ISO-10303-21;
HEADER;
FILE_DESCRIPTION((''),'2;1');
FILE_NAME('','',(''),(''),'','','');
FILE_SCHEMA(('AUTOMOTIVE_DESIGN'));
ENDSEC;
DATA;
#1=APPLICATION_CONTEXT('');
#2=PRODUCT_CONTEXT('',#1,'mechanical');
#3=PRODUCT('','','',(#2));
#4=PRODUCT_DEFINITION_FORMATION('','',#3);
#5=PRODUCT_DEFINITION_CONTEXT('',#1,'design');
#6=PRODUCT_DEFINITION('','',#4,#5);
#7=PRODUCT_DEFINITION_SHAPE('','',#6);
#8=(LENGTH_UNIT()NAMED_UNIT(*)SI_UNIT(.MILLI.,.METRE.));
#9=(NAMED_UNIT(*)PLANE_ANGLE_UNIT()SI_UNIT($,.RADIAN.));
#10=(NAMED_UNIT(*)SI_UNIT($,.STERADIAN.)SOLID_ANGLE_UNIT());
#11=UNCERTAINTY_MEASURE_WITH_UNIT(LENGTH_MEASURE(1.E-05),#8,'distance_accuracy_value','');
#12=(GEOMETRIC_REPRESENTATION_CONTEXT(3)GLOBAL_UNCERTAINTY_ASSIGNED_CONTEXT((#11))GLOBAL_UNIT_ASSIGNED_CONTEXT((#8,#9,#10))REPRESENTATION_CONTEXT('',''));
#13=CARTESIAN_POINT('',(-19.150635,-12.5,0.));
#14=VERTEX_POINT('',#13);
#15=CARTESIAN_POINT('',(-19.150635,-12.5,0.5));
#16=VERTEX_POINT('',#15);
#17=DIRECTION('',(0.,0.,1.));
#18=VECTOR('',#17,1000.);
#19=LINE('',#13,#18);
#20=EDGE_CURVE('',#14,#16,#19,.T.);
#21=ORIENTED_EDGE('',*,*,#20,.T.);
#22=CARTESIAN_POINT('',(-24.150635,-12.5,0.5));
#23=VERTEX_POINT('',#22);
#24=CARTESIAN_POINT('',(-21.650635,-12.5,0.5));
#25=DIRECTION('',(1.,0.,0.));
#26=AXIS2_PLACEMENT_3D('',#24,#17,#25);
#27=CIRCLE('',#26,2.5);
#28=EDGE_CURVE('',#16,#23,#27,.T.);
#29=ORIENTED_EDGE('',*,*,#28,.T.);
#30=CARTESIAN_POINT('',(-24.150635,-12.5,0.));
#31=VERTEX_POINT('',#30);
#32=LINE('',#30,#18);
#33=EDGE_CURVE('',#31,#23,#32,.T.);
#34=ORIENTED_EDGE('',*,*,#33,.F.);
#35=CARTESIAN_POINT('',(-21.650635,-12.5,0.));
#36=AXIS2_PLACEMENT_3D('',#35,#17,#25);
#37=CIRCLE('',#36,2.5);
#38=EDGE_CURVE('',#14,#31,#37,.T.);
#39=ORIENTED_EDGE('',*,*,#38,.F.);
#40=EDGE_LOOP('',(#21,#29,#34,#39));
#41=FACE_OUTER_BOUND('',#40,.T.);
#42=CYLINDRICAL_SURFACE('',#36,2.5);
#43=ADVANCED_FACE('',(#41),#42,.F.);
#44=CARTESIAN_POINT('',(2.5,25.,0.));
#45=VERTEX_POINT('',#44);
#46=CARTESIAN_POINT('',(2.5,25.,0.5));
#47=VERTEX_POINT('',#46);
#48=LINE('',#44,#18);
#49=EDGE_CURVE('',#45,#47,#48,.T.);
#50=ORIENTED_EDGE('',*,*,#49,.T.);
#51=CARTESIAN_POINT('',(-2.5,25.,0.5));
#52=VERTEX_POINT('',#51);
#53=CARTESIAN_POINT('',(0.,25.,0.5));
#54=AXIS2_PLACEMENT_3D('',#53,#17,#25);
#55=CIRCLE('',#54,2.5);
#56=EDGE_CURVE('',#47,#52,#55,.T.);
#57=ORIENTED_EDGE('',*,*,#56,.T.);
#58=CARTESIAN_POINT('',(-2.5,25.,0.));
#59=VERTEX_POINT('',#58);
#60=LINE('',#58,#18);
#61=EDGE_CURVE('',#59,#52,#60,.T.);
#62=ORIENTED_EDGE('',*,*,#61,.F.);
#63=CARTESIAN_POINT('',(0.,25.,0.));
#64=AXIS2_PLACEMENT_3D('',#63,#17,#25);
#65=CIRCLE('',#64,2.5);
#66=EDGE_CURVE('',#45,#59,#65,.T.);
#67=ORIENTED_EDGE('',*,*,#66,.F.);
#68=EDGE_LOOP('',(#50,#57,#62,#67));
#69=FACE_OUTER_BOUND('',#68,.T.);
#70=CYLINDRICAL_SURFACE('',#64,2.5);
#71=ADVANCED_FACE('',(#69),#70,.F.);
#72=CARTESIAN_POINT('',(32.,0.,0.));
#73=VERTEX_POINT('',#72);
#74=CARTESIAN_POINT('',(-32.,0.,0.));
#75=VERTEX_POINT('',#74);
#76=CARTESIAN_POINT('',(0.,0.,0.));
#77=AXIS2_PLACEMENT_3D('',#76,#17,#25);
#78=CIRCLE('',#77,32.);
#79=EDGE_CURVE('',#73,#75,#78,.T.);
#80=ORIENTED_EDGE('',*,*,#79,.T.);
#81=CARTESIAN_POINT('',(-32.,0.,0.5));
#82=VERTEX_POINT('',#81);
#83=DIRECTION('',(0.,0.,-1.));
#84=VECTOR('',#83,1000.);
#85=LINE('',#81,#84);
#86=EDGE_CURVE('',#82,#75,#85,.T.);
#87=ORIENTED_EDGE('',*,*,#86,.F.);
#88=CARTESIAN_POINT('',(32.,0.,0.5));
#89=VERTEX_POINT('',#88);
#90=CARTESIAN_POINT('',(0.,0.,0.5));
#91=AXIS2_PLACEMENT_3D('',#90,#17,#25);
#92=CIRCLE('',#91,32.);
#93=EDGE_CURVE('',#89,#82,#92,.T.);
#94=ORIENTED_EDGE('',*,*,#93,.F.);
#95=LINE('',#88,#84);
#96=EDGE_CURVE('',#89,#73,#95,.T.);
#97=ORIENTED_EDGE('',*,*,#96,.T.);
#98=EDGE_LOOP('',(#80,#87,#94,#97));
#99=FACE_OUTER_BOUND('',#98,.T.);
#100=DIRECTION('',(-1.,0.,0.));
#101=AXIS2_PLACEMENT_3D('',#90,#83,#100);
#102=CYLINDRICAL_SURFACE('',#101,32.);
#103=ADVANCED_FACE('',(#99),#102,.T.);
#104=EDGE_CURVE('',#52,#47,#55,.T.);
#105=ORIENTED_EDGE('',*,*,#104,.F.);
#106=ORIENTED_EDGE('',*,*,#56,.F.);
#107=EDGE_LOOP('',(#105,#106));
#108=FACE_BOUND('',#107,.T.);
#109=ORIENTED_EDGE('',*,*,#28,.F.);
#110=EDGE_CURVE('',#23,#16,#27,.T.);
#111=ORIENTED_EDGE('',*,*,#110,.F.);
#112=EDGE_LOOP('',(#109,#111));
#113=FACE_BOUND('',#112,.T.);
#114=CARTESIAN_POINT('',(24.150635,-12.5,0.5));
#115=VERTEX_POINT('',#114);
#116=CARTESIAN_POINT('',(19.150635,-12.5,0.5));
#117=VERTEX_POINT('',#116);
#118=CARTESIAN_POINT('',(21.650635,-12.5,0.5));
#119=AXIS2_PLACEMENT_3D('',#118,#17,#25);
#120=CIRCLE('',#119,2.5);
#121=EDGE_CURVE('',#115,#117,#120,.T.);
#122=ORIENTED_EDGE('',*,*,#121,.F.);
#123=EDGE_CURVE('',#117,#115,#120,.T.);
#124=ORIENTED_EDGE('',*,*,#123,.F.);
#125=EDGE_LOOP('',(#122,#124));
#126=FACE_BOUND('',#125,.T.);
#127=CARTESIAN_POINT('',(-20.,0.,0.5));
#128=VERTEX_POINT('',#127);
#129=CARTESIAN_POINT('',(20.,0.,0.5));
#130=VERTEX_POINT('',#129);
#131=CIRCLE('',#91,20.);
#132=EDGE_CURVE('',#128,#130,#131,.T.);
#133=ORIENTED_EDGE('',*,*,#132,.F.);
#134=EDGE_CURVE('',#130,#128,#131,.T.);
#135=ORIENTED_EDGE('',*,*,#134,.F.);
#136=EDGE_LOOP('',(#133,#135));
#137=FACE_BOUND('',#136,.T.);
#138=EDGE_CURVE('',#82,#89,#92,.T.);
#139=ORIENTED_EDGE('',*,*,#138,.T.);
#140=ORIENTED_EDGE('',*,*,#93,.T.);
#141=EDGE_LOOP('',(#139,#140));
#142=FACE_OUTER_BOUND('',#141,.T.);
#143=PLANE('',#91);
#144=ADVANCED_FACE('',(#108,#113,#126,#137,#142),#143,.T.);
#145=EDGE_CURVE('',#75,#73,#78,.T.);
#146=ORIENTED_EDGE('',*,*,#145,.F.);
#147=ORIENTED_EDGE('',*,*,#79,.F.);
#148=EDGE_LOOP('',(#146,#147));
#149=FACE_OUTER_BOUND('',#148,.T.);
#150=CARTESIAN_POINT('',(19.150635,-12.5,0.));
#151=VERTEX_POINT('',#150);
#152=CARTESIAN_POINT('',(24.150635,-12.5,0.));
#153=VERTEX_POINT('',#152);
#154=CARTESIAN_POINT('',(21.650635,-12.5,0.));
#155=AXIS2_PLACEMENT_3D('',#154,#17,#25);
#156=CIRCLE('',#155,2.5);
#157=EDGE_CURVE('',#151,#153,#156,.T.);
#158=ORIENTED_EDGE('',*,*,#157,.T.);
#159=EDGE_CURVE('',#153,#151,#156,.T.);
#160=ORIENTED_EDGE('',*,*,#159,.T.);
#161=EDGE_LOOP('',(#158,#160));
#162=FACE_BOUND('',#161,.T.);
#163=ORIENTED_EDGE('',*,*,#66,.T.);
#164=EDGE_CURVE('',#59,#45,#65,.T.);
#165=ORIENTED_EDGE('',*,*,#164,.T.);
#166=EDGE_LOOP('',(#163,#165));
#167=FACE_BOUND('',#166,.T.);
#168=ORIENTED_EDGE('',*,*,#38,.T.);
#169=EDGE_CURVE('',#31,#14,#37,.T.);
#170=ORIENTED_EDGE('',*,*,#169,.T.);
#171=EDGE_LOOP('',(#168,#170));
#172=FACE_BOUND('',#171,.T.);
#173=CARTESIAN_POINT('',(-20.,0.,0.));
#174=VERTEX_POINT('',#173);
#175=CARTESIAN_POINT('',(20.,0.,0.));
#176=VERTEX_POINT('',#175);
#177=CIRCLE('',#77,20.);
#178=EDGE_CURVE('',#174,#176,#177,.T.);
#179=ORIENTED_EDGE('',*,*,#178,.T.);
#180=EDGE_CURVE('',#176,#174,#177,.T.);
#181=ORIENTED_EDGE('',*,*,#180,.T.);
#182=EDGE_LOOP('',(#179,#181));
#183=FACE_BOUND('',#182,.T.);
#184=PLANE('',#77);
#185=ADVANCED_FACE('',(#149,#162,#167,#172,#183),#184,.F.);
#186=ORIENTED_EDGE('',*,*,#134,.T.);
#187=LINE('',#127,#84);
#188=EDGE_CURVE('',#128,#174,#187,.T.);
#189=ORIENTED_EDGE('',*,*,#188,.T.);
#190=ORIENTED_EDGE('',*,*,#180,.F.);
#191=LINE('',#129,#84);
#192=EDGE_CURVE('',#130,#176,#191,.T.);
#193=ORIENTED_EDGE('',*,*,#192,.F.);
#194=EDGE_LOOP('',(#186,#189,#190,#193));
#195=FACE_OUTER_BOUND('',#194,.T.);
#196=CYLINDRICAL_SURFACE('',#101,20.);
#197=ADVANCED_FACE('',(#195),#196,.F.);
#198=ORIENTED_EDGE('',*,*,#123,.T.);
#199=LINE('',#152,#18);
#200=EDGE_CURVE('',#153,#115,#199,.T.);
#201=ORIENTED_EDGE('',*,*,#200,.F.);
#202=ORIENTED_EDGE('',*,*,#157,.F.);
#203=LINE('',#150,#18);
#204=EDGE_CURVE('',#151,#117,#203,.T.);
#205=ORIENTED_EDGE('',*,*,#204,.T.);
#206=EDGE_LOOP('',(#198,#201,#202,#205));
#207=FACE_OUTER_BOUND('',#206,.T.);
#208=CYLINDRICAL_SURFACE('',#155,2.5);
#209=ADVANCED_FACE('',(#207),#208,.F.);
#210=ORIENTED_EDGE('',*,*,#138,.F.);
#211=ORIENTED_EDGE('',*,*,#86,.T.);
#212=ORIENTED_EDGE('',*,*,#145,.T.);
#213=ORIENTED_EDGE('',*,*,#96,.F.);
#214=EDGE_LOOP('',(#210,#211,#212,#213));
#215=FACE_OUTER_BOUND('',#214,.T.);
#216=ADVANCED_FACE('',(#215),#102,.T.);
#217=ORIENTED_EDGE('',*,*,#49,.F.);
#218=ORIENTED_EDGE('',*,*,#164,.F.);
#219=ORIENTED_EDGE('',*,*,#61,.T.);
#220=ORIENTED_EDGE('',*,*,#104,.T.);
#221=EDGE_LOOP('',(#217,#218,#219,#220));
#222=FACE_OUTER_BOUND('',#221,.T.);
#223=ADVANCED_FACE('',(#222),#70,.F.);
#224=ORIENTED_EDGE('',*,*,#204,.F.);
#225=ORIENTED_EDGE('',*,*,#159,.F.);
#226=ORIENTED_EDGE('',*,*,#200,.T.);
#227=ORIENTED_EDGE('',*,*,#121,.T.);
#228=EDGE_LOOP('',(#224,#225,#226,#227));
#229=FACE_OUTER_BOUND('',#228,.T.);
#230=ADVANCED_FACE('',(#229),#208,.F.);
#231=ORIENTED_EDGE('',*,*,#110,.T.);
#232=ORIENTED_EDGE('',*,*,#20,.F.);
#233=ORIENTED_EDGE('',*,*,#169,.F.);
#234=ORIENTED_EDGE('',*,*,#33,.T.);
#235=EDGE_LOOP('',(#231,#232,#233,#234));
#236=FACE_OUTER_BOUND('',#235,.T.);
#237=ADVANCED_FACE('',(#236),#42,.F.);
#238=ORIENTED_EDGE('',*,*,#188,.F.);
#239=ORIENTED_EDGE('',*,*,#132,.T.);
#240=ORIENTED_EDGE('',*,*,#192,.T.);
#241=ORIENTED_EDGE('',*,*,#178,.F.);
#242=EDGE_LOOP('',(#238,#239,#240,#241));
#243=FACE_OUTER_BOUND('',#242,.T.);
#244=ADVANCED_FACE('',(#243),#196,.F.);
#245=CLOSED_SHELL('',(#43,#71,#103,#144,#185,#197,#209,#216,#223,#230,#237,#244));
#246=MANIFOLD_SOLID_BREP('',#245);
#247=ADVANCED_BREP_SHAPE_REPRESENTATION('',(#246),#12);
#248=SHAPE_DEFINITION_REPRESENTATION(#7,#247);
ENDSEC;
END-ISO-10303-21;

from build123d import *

# Parameters (mm, degrees)
SKETCH1_R           = 32
SKETCH1_R_2         = 20
BOSS_EXTRUDE1_DEPTH = 0.5
SKETCH2_R           = 2.5
CUT_EXTRUDE1_DEPTH  = 0.5


with BuildPart() as part:
    # Sketch1 → Boss-Extrude1 (new body)
    with BuildSketch(Plane.XY):
        Circle(SKETCH1_R)
        Circle(SKETCH1_R_2, mode=Mode.SUBTRACT)
    extrude(amount=BOSS_EXTRUDE1_DEPTH)

    # Sketch2 → Cut-Extrude1 (cut)
    with BuildSketch(Plane.XY.offset(0.5)):
        with Locations((0, 25)):
            Circle(SKETCH2_R)
        with Locations((21.650635095, -12.5)):
            Circle(SKETCH2_R)
        with Locations((-21.650635095, -12.5)):
            Circle(SKETCH2_R)
    extrude(amount=-CUT_EXTRUDE1_DEPTH, mode=Mode.SUBTRACT)


solid = part.part
